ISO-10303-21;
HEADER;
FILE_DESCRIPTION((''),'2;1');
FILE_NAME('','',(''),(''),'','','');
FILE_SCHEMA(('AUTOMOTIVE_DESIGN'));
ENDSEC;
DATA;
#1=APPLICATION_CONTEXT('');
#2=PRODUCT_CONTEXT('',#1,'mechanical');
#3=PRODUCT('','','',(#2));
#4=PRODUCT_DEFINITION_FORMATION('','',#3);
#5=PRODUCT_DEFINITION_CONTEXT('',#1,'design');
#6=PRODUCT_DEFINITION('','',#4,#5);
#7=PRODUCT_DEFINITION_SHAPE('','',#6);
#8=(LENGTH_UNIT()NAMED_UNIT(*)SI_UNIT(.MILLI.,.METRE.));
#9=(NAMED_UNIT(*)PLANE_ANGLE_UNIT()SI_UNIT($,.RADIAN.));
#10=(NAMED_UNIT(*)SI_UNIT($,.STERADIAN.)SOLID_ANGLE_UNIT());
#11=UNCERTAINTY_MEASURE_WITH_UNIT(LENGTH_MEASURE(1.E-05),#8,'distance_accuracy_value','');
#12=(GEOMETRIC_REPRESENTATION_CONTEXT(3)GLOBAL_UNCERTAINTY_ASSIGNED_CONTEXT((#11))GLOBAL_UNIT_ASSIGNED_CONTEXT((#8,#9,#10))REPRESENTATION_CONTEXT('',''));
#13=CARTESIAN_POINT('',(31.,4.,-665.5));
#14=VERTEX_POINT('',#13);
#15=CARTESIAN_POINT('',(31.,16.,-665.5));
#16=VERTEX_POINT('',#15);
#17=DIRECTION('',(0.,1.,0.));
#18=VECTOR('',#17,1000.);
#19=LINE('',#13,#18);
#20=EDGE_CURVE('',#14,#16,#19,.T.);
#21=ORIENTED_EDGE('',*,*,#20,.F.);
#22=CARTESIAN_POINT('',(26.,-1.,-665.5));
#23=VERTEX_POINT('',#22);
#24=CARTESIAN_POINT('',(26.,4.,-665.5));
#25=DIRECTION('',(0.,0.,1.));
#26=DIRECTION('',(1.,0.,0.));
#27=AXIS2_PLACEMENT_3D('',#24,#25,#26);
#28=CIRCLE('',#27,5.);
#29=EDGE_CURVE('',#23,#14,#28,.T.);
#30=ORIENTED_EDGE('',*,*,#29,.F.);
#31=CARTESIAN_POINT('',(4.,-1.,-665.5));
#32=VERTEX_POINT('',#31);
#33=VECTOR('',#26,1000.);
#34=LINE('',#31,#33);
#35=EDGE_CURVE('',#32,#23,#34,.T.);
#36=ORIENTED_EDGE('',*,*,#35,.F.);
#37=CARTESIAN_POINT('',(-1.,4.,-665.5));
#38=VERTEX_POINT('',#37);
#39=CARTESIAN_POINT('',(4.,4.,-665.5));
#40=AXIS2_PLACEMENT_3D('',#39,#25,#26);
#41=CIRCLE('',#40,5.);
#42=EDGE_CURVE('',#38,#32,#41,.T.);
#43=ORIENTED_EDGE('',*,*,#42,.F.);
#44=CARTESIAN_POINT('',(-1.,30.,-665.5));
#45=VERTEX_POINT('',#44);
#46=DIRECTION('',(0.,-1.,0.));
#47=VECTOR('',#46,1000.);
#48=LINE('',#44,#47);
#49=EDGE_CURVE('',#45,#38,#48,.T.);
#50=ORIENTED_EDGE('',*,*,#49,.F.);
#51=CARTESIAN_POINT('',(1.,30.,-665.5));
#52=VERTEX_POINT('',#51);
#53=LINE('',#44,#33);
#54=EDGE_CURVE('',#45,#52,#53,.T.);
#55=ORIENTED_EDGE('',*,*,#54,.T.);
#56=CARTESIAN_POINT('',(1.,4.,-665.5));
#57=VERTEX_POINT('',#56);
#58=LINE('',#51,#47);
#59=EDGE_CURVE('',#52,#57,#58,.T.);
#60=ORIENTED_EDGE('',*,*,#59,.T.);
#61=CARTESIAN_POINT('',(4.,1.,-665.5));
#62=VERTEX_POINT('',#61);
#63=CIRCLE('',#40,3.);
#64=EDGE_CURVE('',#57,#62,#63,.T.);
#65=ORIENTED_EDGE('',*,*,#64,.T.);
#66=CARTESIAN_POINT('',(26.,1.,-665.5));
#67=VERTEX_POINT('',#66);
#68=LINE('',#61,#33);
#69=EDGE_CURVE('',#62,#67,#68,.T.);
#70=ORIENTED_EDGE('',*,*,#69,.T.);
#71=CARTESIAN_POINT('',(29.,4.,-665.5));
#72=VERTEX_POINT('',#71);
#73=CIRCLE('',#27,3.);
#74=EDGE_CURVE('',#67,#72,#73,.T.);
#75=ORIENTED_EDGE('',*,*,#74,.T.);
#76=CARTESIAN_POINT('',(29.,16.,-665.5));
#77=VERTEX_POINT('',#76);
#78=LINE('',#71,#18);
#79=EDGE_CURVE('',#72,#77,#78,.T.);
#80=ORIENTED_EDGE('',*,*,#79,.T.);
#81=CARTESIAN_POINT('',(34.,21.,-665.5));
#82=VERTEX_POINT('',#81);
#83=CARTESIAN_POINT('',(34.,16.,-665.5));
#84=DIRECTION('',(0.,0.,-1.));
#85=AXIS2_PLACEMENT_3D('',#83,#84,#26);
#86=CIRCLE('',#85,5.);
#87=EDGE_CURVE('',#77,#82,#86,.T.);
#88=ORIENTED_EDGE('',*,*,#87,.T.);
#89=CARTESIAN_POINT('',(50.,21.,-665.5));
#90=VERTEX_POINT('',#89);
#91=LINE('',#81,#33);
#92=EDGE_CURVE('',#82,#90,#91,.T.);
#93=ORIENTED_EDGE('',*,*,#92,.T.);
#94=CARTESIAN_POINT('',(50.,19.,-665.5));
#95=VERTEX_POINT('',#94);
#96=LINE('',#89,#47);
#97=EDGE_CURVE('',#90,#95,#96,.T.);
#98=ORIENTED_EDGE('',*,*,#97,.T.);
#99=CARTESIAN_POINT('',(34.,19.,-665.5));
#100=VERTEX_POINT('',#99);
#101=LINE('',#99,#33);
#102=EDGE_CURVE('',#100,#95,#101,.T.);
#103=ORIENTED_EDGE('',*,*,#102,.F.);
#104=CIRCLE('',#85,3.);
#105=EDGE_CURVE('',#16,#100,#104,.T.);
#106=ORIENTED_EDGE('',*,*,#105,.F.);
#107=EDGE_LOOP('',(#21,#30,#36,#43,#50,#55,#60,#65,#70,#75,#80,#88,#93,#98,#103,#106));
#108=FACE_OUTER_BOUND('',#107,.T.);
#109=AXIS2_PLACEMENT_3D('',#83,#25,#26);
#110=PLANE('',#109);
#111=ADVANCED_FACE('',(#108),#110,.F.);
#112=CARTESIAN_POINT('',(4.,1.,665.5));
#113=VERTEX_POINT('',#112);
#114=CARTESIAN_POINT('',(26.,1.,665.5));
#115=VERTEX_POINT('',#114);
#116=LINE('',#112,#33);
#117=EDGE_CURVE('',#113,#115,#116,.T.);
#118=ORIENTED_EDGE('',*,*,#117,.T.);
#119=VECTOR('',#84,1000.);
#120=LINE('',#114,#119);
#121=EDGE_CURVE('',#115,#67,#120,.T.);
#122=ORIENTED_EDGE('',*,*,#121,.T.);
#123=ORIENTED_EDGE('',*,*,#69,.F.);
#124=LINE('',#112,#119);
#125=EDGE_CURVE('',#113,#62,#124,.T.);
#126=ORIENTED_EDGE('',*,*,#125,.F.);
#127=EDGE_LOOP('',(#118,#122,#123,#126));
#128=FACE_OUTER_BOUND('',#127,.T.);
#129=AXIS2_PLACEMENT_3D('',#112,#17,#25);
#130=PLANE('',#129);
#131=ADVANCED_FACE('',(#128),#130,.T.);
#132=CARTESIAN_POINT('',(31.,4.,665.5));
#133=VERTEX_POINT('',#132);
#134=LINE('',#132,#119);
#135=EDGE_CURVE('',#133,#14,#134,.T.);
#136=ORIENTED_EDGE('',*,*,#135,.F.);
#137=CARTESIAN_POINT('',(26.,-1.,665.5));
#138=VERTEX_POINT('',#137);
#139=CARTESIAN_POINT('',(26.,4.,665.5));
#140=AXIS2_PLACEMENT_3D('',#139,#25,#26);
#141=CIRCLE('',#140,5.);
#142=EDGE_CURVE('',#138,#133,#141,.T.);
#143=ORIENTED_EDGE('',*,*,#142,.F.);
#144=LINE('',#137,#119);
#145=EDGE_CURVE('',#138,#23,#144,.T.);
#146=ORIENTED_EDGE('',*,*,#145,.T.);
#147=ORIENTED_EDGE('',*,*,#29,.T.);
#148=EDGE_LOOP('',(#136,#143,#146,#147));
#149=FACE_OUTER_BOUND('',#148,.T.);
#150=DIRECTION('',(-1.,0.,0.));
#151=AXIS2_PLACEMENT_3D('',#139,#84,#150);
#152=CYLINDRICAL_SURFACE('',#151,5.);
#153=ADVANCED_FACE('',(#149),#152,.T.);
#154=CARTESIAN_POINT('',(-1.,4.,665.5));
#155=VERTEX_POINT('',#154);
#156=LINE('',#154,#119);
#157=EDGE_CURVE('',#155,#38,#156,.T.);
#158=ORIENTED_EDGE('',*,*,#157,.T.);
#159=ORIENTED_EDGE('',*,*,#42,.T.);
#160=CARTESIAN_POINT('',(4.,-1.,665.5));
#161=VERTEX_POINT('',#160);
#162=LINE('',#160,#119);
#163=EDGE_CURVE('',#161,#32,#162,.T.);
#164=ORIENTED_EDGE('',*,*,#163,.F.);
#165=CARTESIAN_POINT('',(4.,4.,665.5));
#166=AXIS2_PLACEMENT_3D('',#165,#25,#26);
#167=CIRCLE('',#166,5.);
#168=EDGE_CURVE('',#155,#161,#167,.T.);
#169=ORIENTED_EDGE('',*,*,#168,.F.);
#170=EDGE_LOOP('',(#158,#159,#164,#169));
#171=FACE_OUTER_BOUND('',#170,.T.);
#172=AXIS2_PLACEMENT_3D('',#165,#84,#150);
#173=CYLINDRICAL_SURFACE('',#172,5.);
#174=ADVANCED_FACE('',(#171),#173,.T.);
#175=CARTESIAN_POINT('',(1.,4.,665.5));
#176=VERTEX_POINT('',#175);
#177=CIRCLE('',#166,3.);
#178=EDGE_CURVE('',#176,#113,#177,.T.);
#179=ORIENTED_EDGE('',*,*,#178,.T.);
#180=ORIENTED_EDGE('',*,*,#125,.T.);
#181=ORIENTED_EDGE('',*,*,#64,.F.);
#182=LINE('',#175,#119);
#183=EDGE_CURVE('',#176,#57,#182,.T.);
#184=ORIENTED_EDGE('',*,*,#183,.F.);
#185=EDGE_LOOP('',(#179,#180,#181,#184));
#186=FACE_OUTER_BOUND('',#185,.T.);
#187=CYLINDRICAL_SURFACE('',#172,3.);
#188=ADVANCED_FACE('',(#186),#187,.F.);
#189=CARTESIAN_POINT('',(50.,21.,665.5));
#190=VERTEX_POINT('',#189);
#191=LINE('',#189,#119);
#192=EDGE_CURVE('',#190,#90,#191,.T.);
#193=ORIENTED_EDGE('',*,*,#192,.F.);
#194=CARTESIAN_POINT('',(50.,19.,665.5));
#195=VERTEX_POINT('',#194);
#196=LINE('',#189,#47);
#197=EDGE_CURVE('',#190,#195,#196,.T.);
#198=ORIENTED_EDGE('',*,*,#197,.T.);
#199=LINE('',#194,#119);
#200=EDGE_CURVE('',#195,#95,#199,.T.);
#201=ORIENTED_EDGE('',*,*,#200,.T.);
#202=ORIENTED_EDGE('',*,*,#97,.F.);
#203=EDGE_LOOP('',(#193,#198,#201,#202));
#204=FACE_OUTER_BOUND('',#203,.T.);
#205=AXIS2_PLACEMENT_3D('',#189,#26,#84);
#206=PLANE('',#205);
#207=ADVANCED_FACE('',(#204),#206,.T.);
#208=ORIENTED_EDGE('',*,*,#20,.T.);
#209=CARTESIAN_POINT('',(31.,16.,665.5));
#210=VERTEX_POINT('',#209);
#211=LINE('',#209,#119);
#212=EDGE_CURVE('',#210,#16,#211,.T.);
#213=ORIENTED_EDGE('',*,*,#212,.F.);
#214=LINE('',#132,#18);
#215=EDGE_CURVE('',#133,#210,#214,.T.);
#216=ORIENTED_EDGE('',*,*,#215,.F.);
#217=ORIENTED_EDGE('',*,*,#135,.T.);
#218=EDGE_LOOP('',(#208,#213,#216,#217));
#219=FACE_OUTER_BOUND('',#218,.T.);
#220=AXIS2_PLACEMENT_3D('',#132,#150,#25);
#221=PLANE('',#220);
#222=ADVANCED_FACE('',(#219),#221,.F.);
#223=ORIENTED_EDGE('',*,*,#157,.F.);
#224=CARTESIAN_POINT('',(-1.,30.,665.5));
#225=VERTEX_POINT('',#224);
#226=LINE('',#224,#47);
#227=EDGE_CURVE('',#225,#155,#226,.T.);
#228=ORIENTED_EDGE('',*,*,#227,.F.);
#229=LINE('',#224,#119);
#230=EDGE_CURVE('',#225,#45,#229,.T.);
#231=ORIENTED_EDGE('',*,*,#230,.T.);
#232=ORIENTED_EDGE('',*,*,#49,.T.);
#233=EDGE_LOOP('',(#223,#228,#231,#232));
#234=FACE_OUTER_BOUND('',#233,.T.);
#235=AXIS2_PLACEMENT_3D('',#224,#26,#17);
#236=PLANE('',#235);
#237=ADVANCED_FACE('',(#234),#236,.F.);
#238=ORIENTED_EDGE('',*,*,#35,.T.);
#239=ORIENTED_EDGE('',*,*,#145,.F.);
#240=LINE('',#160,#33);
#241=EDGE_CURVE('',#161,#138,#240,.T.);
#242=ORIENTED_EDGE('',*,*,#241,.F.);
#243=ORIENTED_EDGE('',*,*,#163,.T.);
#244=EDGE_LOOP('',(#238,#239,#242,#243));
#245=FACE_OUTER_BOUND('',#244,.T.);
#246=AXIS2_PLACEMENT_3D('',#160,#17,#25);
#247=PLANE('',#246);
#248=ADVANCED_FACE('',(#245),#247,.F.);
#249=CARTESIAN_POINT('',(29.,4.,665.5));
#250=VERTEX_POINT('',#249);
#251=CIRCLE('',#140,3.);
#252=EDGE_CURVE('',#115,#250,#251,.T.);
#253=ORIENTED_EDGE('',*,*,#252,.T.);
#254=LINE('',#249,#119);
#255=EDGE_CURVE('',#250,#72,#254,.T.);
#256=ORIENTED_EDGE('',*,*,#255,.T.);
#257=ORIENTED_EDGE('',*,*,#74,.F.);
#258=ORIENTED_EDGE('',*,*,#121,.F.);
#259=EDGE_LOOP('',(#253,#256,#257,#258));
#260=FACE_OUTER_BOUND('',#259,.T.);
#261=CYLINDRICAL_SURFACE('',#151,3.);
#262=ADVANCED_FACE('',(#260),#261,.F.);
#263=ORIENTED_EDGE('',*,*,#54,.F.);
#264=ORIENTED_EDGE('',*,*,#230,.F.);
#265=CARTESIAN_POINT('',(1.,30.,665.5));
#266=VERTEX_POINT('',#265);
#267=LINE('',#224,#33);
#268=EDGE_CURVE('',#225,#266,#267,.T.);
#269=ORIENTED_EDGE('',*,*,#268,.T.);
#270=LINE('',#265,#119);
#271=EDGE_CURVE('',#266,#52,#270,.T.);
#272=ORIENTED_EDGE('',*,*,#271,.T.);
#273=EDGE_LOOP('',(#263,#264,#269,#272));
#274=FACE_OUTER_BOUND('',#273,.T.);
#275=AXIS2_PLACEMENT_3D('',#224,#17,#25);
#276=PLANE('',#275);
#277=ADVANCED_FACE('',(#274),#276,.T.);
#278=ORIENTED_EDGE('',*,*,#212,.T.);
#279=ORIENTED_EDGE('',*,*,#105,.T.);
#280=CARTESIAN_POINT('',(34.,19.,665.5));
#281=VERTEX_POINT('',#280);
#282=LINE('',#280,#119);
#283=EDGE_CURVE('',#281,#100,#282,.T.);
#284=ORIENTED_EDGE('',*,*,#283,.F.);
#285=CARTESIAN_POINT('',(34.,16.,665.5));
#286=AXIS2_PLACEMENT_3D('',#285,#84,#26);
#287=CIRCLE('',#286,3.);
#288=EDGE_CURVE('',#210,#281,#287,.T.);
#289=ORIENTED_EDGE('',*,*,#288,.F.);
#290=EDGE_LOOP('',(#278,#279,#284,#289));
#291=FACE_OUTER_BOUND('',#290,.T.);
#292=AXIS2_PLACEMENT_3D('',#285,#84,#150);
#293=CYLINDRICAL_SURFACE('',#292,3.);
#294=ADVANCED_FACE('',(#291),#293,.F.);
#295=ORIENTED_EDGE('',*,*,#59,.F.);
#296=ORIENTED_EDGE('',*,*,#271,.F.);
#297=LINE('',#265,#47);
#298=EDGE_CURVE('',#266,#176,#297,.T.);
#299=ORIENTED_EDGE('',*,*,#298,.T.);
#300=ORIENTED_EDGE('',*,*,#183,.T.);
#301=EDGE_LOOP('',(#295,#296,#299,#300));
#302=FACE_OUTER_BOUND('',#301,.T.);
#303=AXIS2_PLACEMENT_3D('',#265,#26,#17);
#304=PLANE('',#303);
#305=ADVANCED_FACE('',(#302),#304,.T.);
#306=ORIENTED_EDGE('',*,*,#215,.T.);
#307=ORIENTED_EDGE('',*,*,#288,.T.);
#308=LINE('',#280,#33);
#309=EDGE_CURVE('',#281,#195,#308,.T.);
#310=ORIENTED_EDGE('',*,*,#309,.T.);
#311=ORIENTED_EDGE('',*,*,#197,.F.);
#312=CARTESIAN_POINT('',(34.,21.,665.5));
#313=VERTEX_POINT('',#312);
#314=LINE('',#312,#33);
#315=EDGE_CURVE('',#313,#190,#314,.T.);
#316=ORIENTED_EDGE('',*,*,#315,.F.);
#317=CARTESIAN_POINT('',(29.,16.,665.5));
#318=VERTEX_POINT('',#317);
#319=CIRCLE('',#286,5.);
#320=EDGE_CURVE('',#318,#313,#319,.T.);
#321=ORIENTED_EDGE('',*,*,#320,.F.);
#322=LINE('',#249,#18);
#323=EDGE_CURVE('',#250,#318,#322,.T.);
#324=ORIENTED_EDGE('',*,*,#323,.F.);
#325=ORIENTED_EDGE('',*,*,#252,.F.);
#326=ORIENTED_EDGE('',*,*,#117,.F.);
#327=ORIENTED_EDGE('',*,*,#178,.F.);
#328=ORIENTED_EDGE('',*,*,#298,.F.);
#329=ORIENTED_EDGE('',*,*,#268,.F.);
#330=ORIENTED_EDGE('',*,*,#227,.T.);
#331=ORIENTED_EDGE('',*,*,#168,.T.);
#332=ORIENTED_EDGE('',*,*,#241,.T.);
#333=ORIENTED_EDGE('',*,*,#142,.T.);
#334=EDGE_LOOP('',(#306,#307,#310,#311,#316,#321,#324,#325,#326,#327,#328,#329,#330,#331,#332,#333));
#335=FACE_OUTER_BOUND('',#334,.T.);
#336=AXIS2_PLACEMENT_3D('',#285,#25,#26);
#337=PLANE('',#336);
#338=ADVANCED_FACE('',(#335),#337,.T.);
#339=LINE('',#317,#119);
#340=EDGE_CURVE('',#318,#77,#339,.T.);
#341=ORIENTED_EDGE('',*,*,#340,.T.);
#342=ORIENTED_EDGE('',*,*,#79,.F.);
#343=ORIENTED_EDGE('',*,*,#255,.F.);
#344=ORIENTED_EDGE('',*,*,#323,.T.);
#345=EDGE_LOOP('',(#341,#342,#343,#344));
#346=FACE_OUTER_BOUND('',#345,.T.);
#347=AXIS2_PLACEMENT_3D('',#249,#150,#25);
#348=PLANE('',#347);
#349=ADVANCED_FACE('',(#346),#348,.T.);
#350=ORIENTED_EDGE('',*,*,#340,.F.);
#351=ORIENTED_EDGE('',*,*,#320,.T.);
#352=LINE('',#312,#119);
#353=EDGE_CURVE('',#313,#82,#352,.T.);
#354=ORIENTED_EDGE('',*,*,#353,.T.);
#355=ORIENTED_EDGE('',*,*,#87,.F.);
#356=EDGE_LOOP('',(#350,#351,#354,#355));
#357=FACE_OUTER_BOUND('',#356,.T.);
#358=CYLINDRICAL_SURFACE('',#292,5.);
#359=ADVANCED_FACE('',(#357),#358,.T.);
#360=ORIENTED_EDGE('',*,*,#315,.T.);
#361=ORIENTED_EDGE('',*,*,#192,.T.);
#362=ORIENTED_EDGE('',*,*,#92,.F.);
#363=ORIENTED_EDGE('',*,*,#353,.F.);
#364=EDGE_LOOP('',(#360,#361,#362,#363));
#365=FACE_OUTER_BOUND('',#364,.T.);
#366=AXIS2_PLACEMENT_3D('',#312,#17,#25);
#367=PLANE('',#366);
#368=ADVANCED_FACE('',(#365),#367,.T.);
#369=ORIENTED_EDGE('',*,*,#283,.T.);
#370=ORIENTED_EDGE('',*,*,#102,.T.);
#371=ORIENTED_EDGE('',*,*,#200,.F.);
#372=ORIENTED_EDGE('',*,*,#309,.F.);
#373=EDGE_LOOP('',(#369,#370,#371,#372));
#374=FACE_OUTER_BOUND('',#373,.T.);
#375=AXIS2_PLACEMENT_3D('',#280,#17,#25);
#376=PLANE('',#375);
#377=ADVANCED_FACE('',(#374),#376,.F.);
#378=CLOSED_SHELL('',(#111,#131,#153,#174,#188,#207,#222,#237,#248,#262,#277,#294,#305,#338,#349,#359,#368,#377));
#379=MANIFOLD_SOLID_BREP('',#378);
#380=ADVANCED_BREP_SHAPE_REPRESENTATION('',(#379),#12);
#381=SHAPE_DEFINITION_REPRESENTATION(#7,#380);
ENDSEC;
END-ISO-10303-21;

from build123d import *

# Parameters (mm, degrees)
EXTRUDE_1_DEPTH = 665.5


with BuildPart() as part:
    # 草图1 → 拉伸-薄壁1 (new, symmetric)
    with BuildSketch(Plane.XY):
        with BuildLine():
            Line((-1, 30), (-1, 4))
            ThreePointArc((-1, 4), (0.464466094, 0.464466094), (4, -1))
            Line((4, -1), (26, -1))
            ThreePointArc((26, -1), (29.535533906, 0.464466094), (31, 4))
            Line((31, 4), (31, 16))
            ThreePointArc((31, 16), (31.878679656, 18.121320344), (34, 19))
            Line((34, 19), (50, 19))
            Line((50, 19), (50, 21))
            Line((50, 21), (34, 21))
            ThreePointArc((34, 21), (30.464466094, 19.535533906), (29, 16))
            Line((29, 16), (29, 4))
            ThreePointArc((29, 4), (28.121320344, 1.878679656), (26, 1))
            Line((26, 1), (4, 1))
            ThreePointArc((4, 1), (1.878679656, 1.878679656), (1, 4))
            Line((1, 4), (1, 30))
            Line((1, 30), (-1, 30))
        make_face()
    extrude(amount=EXTRUDE_1_DEPTH, both=True)


solid = part.part
